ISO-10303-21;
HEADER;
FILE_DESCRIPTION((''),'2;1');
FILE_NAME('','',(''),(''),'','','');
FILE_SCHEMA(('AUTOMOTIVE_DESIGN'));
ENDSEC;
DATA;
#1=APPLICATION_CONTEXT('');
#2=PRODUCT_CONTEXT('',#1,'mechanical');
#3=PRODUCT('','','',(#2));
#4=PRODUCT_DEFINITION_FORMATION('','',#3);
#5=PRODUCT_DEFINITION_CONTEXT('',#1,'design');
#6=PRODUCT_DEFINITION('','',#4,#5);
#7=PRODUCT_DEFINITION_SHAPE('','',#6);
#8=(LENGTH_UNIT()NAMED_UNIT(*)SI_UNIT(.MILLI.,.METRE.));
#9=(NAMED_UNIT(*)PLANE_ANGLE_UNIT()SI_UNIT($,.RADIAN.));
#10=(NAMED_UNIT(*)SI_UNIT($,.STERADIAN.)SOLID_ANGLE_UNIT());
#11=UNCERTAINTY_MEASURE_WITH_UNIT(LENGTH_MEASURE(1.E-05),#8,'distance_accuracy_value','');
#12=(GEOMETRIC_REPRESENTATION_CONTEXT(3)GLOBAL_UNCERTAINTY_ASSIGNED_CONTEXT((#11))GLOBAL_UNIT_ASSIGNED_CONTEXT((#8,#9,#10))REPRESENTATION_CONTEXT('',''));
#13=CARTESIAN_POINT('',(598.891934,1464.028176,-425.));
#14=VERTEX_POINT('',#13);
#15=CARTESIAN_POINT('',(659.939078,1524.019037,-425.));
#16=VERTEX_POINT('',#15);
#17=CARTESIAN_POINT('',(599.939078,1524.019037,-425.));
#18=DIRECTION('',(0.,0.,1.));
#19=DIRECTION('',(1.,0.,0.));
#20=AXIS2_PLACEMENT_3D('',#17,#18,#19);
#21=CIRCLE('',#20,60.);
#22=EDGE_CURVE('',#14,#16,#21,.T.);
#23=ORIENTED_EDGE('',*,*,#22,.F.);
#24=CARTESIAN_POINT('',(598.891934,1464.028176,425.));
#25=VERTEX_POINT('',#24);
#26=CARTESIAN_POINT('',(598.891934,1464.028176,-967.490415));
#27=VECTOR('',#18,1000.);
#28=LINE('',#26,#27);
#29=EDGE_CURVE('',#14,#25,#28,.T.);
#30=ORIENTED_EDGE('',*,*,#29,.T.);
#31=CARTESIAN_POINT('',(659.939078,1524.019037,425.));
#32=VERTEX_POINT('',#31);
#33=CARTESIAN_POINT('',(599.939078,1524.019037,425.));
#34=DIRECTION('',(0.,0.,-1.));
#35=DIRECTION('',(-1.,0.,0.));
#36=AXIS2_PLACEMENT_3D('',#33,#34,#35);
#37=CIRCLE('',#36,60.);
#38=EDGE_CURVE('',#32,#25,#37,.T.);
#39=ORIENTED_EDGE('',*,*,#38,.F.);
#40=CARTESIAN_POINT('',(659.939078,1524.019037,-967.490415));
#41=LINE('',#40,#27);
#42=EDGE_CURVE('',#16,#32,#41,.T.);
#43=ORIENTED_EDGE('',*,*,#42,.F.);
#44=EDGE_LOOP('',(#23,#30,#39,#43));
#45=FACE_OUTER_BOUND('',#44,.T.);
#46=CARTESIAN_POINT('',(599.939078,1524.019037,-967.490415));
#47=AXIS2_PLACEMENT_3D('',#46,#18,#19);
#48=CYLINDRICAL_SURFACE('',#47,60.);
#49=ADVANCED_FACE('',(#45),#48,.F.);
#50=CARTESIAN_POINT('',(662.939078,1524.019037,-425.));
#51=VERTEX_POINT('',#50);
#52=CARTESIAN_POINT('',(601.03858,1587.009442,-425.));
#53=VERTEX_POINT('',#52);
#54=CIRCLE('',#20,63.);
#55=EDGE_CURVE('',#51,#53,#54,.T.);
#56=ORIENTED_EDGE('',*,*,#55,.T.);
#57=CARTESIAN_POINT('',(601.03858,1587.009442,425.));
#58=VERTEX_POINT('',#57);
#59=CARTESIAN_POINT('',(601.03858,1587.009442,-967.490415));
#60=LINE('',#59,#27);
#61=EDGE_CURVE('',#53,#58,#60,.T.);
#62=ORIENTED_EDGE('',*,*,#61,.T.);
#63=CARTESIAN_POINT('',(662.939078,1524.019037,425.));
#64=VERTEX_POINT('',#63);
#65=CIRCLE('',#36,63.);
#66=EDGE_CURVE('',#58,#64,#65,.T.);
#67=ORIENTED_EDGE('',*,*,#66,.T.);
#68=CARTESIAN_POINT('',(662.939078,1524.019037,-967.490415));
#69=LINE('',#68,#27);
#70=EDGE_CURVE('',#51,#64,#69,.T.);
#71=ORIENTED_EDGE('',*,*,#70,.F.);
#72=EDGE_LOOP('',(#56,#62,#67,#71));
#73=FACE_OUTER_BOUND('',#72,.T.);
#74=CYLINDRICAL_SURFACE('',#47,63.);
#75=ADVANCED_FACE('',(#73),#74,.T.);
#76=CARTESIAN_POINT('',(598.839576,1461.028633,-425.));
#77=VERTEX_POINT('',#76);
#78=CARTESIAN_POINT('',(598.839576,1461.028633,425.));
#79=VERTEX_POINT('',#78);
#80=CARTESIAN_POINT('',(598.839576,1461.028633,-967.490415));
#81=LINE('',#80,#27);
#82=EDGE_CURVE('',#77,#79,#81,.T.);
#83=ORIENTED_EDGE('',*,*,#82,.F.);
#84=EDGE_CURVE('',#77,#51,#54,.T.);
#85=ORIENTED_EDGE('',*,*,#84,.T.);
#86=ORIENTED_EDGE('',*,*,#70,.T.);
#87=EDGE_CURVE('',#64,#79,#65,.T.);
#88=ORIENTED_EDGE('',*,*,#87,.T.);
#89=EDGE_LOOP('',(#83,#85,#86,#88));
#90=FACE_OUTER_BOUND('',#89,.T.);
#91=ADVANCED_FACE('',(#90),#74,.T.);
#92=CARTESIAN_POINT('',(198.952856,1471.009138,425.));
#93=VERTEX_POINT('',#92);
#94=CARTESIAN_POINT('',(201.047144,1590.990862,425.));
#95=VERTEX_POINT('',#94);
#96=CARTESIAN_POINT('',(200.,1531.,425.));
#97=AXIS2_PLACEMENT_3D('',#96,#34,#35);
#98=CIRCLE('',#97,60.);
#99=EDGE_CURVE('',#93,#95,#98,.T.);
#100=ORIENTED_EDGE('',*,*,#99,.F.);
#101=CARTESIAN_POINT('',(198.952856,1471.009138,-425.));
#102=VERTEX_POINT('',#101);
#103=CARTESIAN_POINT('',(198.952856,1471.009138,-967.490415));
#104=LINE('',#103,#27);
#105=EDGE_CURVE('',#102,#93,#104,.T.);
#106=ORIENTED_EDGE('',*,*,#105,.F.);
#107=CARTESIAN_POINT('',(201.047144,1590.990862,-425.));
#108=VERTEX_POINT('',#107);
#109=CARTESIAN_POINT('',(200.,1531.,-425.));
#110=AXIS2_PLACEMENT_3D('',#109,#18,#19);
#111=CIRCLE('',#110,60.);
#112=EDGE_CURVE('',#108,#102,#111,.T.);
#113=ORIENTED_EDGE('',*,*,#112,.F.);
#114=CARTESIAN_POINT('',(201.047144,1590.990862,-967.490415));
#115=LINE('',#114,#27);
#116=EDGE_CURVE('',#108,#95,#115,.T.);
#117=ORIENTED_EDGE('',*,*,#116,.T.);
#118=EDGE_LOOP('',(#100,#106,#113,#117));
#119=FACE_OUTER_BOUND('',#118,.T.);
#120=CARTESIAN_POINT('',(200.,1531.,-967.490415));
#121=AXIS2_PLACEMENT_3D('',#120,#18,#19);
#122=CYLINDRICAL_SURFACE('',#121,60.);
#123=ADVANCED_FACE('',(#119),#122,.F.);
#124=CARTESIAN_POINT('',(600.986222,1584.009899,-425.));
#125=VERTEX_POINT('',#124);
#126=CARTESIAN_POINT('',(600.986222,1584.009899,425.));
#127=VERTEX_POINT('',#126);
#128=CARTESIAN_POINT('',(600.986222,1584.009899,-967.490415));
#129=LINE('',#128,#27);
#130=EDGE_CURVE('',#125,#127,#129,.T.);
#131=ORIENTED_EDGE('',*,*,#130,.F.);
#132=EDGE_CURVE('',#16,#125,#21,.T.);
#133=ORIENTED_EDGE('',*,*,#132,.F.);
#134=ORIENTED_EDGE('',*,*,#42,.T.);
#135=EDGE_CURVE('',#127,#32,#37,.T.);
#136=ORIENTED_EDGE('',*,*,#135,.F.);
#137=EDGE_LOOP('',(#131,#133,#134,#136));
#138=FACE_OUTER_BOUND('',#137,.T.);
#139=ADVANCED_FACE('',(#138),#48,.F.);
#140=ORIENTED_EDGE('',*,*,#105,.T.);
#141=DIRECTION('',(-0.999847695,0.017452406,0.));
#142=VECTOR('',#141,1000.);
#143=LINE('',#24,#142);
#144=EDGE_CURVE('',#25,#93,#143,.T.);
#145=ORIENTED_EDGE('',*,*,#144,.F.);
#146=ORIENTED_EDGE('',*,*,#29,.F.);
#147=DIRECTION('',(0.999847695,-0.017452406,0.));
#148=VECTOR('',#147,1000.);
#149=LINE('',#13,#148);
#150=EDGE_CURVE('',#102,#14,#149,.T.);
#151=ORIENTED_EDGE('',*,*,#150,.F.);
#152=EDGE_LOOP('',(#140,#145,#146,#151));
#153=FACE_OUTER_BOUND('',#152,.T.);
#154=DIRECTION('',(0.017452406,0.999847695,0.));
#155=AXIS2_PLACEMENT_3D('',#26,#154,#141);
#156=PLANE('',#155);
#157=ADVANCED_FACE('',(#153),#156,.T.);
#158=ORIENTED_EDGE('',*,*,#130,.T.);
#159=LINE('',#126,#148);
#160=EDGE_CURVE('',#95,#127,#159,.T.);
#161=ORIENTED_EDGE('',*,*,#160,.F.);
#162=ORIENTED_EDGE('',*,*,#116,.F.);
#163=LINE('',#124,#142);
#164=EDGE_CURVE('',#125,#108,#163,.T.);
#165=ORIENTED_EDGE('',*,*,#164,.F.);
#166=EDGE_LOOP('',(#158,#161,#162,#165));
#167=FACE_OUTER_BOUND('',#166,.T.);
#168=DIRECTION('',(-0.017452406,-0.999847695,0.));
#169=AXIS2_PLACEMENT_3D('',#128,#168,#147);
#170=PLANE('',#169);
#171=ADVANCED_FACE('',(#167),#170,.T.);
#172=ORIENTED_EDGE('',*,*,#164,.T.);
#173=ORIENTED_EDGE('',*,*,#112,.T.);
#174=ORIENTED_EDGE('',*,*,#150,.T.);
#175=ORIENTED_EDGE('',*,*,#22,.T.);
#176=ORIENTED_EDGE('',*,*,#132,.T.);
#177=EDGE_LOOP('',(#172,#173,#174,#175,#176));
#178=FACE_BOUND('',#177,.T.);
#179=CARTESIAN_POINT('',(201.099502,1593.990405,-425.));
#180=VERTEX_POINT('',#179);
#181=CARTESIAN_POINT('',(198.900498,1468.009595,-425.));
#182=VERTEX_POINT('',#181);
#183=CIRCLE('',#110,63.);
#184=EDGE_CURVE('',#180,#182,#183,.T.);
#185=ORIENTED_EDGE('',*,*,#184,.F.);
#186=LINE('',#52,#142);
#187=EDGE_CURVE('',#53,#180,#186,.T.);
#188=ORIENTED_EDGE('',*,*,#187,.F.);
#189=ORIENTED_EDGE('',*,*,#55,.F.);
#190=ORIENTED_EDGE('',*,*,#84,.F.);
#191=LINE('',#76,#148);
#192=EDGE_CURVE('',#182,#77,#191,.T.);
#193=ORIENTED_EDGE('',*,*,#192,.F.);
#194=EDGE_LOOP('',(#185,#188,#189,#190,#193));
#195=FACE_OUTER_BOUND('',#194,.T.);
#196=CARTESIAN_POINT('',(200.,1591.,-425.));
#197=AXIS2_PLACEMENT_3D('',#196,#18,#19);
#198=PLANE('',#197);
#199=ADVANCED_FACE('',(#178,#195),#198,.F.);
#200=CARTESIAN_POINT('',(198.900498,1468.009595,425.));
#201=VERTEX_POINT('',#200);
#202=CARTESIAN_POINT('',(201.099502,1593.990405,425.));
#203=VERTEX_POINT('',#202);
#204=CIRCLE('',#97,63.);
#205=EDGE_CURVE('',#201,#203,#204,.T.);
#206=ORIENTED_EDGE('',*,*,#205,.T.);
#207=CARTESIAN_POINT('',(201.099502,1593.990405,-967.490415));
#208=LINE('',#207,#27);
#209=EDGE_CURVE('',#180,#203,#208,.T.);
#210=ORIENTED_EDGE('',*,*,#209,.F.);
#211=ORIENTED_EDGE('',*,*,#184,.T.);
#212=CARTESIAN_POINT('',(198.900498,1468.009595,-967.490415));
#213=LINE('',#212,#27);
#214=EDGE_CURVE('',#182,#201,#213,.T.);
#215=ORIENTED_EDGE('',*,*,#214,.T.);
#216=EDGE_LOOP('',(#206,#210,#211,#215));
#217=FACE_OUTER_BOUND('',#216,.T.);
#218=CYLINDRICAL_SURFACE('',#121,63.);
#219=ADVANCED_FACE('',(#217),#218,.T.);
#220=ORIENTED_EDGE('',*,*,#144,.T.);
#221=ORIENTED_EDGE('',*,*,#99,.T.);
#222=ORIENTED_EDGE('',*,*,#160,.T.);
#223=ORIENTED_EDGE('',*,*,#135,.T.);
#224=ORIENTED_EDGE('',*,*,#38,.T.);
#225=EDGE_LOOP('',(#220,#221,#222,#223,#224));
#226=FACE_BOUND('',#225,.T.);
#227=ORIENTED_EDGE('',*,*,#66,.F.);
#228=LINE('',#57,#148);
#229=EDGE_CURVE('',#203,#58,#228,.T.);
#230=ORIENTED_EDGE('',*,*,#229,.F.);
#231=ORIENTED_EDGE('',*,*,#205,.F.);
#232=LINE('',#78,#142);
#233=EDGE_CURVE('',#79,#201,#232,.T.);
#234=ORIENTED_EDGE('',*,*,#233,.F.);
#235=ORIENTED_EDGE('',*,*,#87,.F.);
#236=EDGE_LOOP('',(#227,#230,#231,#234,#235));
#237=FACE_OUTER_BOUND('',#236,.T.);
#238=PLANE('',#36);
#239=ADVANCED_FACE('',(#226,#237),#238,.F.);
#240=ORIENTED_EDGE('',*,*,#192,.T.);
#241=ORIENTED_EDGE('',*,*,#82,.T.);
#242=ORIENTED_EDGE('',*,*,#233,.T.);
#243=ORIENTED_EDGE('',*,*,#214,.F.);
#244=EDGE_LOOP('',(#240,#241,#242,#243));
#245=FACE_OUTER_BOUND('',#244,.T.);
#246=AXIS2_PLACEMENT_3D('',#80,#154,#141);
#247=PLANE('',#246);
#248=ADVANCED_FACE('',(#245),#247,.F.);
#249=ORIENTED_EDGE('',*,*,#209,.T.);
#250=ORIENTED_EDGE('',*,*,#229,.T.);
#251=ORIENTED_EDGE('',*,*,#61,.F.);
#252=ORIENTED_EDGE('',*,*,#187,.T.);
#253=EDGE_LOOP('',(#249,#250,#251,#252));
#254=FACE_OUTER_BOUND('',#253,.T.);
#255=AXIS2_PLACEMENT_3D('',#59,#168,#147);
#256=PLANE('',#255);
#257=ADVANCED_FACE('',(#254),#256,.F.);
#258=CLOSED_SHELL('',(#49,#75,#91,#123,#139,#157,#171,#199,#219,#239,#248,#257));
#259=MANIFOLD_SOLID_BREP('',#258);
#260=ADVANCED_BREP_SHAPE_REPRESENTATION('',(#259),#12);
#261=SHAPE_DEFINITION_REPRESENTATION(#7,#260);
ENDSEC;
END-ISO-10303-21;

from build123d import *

# Parameters (mm, degrees)
EXTRUDE_1_DEPTH = 850


with BuildPart() as part:
    # 草图1 → 凸台-拉伸1 (new body)
    with BuildSketch(Plane(origin=(0, 0, 425), x_dir=(-1, 0, 0), z_dir=(0, 0, -1))):
        with BuildLine():
            Line((-601.038579668, 1587.00944222), (-201.099501606, 1593.990404795))
            ThreePointArc((-201.099501606, 1593.990404795), (-137.009595205, 1532.099501606), (-198.900498394, 1468.009595205))
            Line((-198.900498394, 1468.009595205), (-598.839576457, 1461.02863263))
            ThreePointArc((-598.839576457, 1461.02863263), (-662.929482857, 1522.91953582), (-601.038579668, 1587.00944222))
        make_face()
        with BuildLine():
            Line((-600.986222449, 1584.009899134), (-201.047144386, 1590.990861709))
            ThreePointArc((-201.047144386, 1590.990861709), (-140.009138291, 1532.047144386), (-198.952855614, 1471.009138291))
            Line((-198.952855614, 1471.009138291), (-598.891933676, 1464.028175716))
            ThreePointArc((-598.891933676, 1464.028175716), (-659.929939772, 1522.971893039), (-600.986222449, 1584.009899134))
        make_face(mode=Mode.SUBTRACT)
    extrude(amount=EXTRUDE_1_DEPTH)


solid = part.part
